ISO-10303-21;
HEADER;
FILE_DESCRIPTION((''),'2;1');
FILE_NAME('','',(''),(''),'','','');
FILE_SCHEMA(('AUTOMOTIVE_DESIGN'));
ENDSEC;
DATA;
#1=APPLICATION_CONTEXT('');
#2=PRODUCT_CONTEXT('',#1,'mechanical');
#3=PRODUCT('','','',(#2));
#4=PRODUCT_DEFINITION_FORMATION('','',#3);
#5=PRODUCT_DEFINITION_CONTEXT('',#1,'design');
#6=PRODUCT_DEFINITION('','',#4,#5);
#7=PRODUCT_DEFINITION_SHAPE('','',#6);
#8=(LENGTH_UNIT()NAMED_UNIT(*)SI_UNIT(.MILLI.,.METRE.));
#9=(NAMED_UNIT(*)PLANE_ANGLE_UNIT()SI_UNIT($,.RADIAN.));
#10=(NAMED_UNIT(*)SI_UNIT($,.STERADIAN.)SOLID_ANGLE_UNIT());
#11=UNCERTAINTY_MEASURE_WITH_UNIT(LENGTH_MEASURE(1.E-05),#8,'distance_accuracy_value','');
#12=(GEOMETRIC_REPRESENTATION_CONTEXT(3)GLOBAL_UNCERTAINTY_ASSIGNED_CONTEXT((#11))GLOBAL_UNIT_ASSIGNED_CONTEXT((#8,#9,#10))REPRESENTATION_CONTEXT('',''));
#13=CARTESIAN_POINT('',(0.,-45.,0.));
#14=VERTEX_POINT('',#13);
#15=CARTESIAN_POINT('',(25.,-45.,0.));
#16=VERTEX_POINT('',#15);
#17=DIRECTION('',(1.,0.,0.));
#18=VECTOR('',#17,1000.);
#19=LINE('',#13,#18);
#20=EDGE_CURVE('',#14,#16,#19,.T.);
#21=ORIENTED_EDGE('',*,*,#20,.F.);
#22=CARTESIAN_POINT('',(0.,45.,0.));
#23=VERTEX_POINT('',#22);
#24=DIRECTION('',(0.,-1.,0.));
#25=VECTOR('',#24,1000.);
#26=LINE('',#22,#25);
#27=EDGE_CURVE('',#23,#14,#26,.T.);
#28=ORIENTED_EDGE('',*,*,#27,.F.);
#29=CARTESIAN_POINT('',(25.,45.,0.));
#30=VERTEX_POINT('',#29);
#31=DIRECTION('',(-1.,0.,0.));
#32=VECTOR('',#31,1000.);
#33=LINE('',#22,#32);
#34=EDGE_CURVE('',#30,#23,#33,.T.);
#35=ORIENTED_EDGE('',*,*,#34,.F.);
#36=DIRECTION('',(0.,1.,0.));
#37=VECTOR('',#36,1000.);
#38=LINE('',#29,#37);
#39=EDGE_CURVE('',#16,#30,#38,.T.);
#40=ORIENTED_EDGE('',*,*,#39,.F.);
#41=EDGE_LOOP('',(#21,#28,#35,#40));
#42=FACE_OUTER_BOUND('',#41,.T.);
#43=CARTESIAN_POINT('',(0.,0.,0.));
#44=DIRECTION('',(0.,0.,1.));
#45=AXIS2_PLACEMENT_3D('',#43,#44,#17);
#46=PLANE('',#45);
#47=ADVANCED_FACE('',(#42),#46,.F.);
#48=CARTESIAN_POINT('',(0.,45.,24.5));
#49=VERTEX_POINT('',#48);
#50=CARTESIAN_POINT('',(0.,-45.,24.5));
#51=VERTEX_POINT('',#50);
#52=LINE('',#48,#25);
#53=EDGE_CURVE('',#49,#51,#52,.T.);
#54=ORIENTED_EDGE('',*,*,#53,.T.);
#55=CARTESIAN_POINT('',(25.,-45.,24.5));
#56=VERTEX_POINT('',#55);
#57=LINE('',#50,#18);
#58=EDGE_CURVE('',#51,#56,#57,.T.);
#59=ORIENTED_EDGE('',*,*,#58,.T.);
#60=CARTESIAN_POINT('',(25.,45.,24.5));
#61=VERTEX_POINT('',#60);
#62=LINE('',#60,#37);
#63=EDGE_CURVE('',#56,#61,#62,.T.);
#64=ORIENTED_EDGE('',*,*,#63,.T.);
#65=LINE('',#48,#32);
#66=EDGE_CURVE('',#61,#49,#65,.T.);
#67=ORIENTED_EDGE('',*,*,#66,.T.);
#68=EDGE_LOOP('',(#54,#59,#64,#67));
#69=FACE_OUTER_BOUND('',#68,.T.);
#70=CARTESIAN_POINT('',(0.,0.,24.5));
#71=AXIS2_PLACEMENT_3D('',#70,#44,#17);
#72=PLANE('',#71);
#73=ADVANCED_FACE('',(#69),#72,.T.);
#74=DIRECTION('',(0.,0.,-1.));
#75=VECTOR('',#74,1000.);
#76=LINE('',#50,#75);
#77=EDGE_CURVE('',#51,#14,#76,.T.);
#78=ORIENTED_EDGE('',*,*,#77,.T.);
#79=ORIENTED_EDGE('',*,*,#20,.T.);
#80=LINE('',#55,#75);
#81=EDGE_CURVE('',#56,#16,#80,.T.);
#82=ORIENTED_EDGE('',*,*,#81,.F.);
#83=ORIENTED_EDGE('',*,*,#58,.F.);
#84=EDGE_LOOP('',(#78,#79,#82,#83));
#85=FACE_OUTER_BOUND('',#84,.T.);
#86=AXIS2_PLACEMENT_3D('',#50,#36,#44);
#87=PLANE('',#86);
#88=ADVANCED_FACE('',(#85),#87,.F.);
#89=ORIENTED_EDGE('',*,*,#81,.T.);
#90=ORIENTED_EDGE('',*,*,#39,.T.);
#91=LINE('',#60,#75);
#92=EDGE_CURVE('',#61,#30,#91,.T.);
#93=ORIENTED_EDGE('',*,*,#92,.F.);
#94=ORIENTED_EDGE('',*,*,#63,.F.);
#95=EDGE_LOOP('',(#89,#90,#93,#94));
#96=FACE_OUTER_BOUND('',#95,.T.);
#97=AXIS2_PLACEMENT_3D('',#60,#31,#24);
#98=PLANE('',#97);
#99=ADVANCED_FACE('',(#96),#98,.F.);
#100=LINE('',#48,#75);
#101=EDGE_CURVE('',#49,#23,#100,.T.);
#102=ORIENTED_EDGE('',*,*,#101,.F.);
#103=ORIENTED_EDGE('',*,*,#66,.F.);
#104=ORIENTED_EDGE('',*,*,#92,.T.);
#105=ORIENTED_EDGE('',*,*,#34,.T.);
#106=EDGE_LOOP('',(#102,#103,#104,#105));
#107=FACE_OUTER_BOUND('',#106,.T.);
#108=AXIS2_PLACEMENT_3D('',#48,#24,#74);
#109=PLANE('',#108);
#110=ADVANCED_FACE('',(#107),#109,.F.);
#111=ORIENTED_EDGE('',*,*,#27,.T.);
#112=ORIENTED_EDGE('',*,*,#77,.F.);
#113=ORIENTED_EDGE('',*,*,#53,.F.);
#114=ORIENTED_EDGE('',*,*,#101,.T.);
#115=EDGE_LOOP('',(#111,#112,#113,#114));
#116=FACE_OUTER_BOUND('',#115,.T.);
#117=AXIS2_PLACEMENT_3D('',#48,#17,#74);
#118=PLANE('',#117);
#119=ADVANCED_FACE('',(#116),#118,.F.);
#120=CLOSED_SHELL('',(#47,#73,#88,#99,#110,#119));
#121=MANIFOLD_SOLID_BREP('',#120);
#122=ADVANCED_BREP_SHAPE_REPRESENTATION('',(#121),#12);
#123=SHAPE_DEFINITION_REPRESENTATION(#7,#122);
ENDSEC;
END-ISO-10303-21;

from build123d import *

# Parameters (mm, degrees)
SKETCH_1_W      = 25
SKETCH_1_H      = 90
EXTRUDE_1_DEPTH = 24.5


with BuildPart() as part:
    # 草图1 → 凸台-拉伸1 (new body)
    with BuildSketch(Plane.XY):
        with Locations((12.5, 0)):
            Rectangle(SKETCH_1_W, SKETCH_1_H)
    extrude(amount=EXTRUDE_1_DEPTH)


solid = part.part
